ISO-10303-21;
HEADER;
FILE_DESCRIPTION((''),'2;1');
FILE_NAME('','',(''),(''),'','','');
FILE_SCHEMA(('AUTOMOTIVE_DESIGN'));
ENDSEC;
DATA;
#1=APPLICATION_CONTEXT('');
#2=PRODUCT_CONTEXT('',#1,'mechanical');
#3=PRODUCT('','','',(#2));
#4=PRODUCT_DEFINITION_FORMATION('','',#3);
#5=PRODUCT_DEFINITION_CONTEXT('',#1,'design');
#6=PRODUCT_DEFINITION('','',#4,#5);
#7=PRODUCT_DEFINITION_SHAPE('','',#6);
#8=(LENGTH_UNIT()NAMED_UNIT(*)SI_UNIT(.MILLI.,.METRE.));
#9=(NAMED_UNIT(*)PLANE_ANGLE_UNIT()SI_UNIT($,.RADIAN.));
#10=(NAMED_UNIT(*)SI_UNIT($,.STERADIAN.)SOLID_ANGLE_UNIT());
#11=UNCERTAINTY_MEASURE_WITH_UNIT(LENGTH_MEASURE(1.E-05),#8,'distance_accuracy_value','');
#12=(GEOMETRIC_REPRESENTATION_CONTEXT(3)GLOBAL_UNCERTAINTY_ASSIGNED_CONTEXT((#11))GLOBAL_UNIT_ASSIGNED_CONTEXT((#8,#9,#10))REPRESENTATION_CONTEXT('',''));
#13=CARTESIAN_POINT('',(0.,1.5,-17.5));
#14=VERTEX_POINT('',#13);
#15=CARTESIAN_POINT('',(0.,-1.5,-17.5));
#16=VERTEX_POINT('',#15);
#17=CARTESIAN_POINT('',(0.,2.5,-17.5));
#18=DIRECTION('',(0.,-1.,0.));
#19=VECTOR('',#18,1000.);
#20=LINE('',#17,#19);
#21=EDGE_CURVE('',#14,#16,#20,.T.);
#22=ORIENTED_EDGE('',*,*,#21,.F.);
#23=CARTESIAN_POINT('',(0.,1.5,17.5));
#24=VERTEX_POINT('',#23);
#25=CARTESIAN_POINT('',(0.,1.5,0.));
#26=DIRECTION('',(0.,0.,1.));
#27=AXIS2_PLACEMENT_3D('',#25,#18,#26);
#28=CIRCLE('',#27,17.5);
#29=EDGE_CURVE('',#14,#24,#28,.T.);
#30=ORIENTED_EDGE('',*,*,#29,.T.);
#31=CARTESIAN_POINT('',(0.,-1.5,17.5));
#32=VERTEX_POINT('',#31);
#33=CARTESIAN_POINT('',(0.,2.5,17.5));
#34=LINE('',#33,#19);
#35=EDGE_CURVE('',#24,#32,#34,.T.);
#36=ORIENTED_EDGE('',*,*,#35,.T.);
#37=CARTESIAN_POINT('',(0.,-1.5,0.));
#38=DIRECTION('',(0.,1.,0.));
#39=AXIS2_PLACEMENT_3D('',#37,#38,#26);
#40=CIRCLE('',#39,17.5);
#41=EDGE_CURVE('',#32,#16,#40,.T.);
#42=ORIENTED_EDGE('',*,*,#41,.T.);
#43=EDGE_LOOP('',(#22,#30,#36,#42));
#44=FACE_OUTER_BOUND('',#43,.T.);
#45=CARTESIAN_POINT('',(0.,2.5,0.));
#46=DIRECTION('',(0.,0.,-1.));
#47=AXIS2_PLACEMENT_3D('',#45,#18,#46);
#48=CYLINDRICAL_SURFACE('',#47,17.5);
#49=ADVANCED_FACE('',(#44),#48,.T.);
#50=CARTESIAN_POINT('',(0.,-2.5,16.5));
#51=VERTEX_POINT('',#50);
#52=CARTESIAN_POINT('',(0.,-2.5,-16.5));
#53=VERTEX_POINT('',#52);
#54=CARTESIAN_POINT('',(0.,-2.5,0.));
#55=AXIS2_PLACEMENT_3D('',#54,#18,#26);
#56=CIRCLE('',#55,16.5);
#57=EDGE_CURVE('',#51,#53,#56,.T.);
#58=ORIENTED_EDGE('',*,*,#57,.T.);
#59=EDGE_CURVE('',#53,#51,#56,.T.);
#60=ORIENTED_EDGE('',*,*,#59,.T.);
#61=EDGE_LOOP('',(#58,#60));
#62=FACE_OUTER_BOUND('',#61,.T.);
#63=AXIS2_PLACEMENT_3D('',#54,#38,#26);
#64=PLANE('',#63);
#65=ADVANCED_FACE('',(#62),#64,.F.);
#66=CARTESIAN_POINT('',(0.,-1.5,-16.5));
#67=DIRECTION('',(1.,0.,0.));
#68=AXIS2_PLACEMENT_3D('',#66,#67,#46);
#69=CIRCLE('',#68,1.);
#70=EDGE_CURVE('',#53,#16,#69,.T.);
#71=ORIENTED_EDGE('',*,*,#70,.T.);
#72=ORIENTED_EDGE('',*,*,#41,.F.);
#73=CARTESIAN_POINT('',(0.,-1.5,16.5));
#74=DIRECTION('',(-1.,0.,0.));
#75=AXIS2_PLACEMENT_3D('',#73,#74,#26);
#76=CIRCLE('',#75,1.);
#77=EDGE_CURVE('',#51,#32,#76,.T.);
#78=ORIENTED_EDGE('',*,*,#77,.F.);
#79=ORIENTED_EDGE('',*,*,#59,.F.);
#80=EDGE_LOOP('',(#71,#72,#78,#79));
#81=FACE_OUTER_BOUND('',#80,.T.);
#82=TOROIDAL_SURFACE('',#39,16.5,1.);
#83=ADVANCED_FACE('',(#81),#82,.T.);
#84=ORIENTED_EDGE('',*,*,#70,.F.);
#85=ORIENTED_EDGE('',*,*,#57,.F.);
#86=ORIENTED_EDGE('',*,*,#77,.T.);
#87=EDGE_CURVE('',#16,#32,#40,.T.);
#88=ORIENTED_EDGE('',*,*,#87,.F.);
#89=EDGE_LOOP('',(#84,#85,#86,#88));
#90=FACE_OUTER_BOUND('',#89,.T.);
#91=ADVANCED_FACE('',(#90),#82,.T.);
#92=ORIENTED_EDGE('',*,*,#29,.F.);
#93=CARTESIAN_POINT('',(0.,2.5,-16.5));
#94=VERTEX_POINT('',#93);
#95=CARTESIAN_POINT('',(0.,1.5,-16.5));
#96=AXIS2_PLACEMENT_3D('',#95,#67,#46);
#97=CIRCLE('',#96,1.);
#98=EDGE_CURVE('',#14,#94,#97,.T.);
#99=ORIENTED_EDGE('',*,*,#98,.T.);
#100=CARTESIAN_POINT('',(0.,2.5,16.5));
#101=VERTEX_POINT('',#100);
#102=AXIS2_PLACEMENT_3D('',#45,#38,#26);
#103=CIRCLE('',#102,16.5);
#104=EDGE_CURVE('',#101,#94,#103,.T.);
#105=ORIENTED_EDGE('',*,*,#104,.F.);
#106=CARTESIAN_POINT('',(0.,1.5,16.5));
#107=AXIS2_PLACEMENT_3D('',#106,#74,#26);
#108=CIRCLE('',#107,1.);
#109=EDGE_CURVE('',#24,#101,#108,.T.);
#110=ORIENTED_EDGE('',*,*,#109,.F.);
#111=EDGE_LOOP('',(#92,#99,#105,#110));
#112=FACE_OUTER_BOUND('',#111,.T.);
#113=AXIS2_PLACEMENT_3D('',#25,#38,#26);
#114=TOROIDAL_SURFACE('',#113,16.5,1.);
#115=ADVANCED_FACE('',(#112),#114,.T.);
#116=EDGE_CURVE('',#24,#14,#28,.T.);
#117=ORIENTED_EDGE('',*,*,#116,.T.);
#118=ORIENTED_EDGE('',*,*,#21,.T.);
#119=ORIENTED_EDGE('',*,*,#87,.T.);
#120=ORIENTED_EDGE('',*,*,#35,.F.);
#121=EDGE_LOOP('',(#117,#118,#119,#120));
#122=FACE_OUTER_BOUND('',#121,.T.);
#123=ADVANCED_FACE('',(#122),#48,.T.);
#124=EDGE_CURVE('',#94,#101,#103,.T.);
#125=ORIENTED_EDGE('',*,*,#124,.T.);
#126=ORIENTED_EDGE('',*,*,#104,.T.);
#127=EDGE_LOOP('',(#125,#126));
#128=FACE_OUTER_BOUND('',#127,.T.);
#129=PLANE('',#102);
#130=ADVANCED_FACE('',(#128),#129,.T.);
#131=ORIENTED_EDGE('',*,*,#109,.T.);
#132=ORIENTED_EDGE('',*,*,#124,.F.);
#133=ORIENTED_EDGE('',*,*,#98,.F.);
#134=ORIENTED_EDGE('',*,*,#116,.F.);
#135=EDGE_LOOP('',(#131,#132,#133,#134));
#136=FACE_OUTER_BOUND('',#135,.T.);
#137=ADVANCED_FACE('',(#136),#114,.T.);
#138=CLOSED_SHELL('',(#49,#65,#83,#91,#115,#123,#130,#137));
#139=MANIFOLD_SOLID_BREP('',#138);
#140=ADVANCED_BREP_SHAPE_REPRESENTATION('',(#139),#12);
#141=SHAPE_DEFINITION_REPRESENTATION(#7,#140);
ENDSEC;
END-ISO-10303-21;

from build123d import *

# Parameters (mm, degrees)
SKETCH_1_R      = 17.5
EXTRUDE_1_DEPTH = 2.5
FILLET_1_R      = 1


with BuildPart() as part:
    # 草图1 → 凸台-拉伸1 (new, symmetric)
    with BuildSketch(Plane(origin=(0, 0, 0), x_dir=(1, 0, 0), z_dir=(0, 1, 0))):
        with Locations(Location((0, 0, 0), (0, 0, 270))):
            Circle(SKETCH_1_R)
    extrude(amount=EXTRUDE_1_DEPTH, both=True)

    # 圆角1
    fillet_1_edges = [part.edges().sort_by_distance(p)[0] for p in [
        (0, -2.5, -17.5),
        (0, 2.5, -17.5),
    ]]
    fillet(fillet_1_edges, radius=FILLET_1_R)


solid = part.part
